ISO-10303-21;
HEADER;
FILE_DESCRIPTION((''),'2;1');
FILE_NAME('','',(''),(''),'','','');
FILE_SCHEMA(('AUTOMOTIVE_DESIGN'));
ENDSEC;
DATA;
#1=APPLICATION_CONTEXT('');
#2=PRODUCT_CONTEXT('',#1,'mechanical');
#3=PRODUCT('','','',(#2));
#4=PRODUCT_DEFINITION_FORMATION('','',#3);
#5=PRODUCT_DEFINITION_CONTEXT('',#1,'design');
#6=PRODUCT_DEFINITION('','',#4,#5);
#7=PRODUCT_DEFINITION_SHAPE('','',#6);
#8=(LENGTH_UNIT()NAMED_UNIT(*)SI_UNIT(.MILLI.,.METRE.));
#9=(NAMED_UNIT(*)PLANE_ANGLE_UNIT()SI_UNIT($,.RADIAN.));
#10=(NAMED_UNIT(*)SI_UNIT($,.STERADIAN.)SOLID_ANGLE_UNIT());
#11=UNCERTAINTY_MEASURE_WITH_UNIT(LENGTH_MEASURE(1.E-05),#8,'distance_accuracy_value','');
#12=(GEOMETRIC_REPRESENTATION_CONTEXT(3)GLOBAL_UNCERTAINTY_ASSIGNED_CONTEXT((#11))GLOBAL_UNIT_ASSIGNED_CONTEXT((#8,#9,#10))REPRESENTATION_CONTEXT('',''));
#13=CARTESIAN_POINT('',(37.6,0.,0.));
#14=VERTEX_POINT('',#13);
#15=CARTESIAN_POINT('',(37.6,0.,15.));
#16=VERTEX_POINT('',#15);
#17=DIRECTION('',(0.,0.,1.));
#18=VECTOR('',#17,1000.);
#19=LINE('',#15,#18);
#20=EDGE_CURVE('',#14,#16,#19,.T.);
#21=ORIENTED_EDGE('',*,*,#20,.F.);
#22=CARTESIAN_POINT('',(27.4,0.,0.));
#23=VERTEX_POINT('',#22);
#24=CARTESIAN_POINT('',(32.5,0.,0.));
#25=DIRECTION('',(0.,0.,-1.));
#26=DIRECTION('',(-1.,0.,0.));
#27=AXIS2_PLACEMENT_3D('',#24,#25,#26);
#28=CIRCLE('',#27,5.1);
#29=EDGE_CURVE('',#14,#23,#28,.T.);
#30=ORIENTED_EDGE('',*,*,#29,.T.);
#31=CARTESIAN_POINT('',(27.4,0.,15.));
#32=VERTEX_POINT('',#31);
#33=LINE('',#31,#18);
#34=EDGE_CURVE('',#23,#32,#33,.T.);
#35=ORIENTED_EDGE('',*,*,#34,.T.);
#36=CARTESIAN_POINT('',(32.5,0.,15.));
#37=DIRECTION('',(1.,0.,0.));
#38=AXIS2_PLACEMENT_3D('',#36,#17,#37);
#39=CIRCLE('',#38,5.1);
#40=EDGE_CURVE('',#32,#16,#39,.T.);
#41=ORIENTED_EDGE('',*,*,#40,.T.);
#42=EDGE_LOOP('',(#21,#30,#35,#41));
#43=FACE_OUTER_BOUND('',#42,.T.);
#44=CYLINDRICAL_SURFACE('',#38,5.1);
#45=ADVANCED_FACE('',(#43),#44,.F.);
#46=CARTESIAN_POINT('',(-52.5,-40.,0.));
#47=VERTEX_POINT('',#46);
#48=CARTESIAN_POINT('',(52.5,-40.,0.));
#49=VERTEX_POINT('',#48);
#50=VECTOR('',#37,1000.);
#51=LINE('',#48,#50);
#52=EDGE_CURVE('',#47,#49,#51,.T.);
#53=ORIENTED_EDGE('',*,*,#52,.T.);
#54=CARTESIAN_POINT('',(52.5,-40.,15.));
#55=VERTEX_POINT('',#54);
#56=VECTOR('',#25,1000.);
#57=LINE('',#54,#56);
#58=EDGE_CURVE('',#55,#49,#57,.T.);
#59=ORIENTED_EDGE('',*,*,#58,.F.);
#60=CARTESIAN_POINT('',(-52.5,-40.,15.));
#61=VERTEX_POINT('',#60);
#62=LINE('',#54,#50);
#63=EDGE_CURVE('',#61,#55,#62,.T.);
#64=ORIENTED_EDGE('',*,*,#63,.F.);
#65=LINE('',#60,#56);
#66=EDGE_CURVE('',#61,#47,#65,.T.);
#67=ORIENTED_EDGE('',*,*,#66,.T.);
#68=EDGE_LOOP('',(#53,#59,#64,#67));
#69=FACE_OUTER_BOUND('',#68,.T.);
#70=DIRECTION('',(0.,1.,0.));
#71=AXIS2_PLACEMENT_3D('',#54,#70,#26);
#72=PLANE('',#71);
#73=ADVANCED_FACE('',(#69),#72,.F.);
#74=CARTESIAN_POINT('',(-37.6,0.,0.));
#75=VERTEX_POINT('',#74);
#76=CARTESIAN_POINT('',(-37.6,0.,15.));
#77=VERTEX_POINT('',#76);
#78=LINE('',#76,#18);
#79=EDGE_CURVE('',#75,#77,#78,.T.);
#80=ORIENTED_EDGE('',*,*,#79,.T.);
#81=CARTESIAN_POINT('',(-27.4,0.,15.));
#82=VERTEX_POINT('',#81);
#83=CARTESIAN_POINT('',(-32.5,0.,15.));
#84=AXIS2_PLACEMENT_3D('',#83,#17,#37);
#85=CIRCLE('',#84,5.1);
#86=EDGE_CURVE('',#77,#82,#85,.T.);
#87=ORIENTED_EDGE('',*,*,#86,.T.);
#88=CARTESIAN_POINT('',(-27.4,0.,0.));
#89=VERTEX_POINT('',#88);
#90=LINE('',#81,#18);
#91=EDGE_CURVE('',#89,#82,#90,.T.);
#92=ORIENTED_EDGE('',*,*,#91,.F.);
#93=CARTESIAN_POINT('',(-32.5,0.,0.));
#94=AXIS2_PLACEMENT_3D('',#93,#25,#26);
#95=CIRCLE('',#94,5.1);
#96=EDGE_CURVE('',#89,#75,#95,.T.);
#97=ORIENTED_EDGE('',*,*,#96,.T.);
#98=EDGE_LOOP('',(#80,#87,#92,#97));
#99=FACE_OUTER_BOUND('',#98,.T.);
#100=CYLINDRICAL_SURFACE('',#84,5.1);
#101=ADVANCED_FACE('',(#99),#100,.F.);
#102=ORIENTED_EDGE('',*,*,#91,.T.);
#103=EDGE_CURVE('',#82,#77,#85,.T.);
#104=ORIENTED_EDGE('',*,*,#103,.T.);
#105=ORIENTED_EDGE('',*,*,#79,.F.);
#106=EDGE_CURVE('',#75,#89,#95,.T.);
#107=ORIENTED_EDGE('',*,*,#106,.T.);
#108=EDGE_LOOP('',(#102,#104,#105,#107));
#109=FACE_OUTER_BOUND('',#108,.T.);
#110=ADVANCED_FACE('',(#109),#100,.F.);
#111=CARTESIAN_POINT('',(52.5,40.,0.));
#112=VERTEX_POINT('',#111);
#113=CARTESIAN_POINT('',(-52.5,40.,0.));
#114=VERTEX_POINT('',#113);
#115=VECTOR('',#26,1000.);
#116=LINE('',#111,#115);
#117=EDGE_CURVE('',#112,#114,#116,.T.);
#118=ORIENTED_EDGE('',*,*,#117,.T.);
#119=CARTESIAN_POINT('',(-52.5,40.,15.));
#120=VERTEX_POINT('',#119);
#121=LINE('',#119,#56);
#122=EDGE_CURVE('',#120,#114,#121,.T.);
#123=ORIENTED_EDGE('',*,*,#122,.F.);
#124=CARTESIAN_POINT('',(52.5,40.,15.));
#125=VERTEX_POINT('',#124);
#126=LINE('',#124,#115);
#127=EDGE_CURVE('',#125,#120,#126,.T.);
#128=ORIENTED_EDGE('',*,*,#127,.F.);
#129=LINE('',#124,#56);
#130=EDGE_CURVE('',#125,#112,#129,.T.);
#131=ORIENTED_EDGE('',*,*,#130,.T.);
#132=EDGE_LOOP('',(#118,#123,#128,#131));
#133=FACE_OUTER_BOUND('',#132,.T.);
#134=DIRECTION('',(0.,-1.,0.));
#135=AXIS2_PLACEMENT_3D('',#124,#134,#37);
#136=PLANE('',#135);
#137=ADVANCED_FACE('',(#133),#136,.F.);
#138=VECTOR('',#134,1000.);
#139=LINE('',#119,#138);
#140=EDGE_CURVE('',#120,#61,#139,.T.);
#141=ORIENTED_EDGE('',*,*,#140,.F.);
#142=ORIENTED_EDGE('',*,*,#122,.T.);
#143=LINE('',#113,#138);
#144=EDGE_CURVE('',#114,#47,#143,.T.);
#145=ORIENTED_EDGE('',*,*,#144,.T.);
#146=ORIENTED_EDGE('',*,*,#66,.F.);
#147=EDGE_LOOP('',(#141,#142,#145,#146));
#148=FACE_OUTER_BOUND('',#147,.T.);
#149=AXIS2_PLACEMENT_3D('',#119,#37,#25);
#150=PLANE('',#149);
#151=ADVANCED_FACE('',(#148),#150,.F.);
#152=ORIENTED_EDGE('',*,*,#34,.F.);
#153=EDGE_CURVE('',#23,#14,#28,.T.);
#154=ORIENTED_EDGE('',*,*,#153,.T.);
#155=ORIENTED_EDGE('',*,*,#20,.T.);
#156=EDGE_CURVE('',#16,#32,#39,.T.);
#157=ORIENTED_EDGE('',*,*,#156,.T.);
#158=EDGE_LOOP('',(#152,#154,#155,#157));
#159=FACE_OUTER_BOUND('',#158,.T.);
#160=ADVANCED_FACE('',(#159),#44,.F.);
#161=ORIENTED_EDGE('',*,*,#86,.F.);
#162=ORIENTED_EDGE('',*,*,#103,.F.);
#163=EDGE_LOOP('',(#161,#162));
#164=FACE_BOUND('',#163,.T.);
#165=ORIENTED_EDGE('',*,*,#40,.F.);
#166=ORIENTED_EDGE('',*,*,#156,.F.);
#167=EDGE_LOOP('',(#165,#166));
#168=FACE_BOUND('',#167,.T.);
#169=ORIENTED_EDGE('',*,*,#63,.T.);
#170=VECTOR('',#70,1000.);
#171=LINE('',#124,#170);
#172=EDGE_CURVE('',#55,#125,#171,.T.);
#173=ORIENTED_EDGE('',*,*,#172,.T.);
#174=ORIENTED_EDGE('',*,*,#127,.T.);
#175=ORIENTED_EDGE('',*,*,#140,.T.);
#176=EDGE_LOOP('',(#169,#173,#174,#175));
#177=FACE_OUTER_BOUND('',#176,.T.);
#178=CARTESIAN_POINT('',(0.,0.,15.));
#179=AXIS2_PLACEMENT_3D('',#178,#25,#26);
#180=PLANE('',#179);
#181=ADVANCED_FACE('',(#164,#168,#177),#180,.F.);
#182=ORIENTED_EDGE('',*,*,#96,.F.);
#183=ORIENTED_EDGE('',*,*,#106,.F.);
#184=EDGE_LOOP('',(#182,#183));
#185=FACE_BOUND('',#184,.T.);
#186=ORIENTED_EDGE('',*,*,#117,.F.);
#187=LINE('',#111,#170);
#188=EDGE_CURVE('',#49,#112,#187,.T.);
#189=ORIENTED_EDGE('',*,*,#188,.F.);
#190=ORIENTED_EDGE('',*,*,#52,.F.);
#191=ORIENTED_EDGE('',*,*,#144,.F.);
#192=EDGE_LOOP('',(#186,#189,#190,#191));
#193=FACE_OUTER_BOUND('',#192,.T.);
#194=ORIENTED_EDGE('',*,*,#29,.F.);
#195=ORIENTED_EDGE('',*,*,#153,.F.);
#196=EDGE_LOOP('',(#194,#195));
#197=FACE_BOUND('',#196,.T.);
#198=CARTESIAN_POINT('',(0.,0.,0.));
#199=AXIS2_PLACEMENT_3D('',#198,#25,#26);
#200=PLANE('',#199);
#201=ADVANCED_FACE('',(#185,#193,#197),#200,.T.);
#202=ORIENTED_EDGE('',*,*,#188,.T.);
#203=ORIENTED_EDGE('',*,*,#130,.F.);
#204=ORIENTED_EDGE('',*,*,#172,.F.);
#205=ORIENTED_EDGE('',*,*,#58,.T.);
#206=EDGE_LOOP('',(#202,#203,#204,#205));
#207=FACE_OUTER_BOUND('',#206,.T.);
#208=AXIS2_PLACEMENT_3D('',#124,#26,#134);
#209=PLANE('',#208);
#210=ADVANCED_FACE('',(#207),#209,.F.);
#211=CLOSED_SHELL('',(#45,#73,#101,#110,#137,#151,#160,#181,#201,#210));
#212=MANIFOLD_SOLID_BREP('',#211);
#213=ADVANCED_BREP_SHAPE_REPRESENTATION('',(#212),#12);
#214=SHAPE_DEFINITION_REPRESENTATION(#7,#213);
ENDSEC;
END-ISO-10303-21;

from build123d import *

# Parameters (mm, degrees)
SKETCH_1_W              = 105
SKETCH_1_H              = 80
EXTRUDE_1_DEPTH         = 15
HOLE_WIZARD_M12_1_D     = 10.2
HOLE_WIZARD_M12_1_DEPTH = 29.25
HOLE_WIZARD_M12_1_TIP   = 3.064389157


with BuildPart() as part:
    # 草图1 → 凸台-拉伸1 (new body)
    with BuildSketch(Plane.XY):
        Rectangle(SKETCH_1_W, SKETCH_1_H)
    extrude(amount=EXTRUDE_1_DEPTH)

    # M12 螺纹孔1
    with Locations(Plane.XY.offset(15)):
        with Locations((-32.5, 0), (32.5, 0)):
            Hole(HOLE_WIZARD_M12_1_D / 2, depth=HOLE_WIZARD_M12_1_DEPTH)
            with Locations((0, 0, -(HOLE_WIZARD_M12_1_DEPTH + HOLE_WIZARD_M12_1_TIP / 2))):  # 118° drill point
                Cone(0, HOLE_WIZARD_M12_1_D / 2, HOLE_WIZARD_M12_1_TIP, mode=Mode.SUBTRACT)


solid = part.part
